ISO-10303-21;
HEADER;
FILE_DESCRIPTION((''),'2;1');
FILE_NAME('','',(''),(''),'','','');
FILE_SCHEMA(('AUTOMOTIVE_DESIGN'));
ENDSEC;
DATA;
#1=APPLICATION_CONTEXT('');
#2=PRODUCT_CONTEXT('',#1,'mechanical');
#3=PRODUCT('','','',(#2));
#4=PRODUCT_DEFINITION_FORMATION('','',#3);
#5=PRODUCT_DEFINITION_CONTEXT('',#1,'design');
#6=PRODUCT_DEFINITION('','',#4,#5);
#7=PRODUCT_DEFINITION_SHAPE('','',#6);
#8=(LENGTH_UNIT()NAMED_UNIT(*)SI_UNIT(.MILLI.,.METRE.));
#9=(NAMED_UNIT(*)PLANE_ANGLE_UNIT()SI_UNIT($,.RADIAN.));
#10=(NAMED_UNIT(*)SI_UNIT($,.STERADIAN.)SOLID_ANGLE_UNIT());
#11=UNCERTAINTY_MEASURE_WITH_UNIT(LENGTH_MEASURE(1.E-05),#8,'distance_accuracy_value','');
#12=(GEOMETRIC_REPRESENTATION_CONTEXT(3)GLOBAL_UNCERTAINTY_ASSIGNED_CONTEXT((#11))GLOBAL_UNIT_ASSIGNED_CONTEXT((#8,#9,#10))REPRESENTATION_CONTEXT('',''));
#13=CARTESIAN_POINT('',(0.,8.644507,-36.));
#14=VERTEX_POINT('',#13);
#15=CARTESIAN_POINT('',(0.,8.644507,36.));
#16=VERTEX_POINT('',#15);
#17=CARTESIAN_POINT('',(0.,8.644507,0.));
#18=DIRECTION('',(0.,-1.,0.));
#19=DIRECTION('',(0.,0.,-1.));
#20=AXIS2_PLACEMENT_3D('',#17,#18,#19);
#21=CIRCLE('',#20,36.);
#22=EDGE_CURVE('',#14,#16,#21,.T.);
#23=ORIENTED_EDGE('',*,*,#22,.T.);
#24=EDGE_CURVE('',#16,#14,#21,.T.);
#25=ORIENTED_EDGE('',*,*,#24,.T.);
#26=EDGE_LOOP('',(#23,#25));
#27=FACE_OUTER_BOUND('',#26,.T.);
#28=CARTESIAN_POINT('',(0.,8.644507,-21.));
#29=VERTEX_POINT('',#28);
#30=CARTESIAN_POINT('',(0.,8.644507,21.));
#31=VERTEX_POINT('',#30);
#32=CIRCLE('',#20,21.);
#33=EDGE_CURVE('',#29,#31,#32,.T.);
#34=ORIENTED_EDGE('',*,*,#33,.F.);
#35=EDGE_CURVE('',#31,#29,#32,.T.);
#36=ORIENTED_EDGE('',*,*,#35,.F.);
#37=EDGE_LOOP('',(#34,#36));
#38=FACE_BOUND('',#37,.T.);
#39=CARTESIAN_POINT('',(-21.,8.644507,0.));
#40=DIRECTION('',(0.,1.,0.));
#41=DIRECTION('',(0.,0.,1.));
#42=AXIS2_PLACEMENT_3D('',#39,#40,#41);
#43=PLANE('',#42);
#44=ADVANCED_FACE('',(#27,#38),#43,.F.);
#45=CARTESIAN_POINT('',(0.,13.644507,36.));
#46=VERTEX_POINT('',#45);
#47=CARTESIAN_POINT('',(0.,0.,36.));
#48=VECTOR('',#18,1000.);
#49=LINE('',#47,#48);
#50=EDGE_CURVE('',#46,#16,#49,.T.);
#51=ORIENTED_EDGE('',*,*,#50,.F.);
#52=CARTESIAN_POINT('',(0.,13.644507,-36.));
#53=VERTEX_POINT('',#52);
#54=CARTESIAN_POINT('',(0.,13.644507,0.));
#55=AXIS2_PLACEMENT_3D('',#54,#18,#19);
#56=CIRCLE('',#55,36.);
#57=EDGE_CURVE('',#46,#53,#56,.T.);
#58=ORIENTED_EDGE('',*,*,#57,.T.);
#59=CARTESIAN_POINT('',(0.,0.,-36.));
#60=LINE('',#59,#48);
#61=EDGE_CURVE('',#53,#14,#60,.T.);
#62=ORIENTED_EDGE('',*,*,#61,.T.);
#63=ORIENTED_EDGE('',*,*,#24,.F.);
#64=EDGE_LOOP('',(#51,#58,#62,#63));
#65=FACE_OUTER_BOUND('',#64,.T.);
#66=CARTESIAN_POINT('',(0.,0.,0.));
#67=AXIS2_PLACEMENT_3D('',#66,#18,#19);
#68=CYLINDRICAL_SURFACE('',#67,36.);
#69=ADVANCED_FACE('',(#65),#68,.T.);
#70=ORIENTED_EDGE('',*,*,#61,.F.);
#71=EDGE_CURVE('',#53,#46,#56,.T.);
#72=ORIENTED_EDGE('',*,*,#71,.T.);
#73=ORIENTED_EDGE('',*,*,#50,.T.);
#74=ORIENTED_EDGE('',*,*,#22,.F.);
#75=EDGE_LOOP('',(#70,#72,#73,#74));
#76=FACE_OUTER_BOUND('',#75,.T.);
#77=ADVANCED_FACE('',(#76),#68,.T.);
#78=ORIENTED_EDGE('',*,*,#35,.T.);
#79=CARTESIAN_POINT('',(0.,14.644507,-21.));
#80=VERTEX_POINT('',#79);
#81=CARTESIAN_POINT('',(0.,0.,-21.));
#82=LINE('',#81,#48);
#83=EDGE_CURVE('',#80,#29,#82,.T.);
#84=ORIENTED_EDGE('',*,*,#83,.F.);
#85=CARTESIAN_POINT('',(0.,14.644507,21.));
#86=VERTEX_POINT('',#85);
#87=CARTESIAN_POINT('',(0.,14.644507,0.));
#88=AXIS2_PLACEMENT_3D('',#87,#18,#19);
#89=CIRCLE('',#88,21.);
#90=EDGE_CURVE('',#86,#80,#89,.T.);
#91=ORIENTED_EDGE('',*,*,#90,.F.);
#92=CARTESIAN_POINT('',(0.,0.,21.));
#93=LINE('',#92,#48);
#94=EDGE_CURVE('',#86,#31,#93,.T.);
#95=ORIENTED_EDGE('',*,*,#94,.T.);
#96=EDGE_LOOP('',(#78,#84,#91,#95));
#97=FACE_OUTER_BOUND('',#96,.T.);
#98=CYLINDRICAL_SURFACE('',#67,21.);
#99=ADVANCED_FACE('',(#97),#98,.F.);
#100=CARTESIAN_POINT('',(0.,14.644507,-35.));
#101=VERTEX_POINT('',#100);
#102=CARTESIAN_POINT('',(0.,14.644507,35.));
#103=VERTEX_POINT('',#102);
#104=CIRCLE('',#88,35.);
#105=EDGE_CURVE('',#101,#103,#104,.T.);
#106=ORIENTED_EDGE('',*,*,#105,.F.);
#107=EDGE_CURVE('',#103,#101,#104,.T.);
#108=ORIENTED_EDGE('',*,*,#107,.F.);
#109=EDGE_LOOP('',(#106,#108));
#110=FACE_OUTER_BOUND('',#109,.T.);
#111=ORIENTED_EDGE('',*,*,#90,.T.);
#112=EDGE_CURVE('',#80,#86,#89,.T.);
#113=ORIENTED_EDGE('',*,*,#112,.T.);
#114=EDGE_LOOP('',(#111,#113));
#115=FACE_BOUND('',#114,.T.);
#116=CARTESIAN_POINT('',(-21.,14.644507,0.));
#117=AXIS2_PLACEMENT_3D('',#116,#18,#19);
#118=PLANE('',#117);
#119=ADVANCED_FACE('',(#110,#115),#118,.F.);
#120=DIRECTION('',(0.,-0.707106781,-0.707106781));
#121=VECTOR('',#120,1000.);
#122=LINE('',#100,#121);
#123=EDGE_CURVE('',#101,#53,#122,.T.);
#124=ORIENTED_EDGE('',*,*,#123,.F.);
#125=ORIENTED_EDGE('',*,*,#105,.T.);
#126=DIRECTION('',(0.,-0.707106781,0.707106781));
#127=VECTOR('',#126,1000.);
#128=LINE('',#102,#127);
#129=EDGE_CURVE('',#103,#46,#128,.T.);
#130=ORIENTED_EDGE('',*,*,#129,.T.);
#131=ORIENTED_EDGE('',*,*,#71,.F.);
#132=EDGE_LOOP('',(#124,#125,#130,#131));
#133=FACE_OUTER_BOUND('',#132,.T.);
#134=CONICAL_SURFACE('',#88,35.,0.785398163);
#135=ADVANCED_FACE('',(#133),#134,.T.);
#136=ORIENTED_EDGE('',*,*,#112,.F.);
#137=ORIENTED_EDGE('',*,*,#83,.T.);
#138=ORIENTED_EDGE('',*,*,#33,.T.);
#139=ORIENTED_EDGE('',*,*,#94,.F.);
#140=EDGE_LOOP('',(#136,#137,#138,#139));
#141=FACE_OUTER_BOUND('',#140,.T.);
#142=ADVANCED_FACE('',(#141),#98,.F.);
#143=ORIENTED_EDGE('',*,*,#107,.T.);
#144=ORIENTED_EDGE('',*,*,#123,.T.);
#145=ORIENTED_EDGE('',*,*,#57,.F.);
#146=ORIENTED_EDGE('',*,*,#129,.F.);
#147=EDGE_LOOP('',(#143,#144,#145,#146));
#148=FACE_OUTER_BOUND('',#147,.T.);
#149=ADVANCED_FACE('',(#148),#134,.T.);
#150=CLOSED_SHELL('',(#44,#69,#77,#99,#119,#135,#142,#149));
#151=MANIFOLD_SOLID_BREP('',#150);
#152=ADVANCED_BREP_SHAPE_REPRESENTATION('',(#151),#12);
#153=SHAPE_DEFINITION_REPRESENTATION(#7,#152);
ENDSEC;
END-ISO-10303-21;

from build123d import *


with BuildPart() as part:
    # Sketch1 → Base-Revolve (revolve)
    with BuildSketch(Plane.XY, mode=Mode.PRIVATE) as base_revolve_sk:
        Polygon((-35, 14.644507042), (-36, 13.644507042), (-36, 8.644507042), (-21, 8.644507042), (-21, 14.644507042), align=None)
    revolve(base_revolve_sk.sketch.rotate(Axis((0, 0, 0), (0, 1, 0)), 270), axis=Axis((0, 0, 0), (0, 1, 0)))


solid = part.part
